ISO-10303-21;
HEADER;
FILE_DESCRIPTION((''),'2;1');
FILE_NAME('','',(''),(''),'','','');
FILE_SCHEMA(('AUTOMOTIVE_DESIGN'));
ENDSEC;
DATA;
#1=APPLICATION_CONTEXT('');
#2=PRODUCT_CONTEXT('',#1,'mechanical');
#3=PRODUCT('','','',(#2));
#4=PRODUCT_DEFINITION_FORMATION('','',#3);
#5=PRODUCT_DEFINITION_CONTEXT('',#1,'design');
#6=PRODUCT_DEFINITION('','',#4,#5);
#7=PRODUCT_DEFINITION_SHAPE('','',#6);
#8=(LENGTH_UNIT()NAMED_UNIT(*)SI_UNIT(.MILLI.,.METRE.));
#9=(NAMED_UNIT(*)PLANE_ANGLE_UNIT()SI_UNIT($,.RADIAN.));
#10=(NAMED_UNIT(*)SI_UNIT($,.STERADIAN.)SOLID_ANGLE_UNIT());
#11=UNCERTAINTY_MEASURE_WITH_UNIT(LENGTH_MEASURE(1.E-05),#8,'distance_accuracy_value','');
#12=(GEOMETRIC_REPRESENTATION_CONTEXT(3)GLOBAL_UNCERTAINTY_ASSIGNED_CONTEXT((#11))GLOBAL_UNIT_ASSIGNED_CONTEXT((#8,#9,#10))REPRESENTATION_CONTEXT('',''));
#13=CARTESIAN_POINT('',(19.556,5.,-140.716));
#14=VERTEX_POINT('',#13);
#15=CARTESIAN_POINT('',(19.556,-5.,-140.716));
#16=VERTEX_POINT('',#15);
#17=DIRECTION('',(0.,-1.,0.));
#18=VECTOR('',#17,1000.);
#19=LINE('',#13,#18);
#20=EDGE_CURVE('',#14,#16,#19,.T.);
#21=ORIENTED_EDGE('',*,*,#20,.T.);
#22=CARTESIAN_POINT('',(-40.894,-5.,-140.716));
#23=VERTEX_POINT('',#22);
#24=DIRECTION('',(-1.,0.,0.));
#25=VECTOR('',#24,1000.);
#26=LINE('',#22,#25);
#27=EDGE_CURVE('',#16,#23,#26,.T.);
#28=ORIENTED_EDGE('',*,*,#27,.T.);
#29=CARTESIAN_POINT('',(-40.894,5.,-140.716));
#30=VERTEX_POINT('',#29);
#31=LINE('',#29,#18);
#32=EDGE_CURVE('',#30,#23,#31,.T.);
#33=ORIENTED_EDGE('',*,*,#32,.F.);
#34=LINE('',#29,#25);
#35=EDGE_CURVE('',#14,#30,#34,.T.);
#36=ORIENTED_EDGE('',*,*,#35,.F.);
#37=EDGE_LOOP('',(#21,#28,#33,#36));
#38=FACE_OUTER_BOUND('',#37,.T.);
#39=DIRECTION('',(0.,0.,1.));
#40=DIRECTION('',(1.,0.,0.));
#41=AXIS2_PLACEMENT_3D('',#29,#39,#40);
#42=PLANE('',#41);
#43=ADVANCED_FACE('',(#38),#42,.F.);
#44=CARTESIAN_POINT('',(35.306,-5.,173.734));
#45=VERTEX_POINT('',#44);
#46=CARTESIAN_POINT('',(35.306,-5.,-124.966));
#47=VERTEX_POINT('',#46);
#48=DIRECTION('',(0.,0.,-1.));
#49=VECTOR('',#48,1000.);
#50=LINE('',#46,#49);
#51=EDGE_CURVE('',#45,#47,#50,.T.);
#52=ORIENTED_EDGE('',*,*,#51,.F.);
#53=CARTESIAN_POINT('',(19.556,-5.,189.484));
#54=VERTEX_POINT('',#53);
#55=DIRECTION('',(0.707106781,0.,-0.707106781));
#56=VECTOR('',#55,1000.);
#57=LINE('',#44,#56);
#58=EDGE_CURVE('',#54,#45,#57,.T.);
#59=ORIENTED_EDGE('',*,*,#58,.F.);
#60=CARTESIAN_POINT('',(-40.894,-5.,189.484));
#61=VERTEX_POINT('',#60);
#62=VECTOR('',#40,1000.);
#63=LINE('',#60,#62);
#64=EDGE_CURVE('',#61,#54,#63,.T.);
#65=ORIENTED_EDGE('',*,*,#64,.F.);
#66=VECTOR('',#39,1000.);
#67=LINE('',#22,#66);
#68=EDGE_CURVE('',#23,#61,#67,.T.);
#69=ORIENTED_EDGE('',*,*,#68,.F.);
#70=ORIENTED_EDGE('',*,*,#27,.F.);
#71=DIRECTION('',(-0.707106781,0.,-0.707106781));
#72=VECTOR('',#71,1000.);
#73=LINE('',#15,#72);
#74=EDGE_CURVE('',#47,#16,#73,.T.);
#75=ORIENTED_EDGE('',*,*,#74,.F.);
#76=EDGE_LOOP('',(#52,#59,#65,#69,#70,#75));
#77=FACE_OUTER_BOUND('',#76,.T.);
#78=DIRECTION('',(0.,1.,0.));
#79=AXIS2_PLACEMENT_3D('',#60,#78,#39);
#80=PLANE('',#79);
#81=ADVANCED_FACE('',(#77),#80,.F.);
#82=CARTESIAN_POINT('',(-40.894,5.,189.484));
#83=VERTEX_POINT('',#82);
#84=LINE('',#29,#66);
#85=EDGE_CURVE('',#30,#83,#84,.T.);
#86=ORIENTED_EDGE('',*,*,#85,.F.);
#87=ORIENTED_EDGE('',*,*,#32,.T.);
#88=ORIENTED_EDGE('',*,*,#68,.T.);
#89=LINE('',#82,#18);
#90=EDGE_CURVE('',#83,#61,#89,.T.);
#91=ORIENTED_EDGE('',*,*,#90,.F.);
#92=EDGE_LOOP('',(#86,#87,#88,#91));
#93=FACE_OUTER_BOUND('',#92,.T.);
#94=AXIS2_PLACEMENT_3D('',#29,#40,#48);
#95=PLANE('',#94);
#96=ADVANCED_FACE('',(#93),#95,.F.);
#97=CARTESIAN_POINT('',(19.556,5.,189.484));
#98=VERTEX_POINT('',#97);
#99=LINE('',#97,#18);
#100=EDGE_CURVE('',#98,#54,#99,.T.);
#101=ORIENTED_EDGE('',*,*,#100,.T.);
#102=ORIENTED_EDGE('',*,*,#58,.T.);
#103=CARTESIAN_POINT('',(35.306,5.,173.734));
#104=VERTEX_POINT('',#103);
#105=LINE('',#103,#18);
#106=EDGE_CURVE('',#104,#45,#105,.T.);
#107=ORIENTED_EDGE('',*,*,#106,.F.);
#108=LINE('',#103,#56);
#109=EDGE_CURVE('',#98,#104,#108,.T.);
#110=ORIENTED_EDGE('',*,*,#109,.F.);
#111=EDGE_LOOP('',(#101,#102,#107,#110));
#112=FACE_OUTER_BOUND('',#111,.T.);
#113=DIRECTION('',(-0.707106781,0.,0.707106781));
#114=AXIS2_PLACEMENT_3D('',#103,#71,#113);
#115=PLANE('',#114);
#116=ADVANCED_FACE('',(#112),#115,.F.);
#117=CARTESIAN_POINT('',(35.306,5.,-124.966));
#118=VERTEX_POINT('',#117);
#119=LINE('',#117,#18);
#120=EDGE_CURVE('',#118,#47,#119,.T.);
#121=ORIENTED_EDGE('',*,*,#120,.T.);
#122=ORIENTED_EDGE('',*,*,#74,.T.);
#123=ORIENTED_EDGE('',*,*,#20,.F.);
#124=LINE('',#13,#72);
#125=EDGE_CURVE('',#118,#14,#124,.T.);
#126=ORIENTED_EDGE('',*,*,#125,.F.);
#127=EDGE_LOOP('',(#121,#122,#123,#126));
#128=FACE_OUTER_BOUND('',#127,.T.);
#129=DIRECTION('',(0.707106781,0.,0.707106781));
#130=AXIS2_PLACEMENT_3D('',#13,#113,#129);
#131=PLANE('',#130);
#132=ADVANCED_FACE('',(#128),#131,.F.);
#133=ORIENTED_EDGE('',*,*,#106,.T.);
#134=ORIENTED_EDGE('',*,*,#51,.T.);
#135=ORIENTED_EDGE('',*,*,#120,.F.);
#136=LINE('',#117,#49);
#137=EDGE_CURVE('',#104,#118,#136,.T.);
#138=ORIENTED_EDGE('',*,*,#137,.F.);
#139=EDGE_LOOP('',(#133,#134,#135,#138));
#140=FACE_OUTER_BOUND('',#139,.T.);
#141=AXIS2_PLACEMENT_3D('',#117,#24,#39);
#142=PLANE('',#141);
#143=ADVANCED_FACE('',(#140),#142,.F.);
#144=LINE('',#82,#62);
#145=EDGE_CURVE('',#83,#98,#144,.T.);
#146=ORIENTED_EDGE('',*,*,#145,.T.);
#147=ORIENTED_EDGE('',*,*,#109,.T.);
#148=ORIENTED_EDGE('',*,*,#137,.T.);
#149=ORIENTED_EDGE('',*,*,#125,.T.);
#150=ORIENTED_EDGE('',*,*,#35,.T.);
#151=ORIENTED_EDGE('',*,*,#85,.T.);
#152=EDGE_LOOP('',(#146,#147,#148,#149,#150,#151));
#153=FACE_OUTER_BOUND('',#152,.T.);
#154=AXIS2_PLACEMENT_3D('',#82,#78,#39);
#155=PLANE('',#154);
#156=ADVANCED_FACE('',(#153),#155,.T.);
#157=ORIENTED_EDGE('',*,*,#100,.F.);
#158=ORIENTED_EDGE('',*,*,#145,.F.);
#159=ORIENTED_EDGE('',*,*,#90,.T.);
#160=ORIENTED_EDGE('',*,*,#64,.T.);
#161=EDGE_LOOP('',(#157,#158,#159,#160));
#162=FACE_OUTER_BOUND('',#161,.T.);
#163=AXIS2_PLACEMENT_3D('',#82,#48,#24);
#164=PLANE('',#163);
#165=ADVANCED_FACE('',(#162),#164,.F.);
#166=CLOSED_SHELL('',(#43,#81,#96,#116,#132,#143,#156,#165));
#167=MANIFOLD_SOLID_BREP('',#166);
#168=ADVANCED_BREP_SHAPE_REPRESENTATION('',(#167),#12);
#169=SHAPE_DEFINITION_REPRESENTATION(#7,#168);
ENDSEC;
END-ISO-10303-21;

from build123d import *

# Parameters (mm, degrees)
BOSS_EXTRUDE1_DEPTH = 5


with BuildPart() as part:
    # Sketch3 → Boss-Extrude1 (new, symmetric)
    with BuildSketch(Plane(origin=(0, 0, 0), x_dir=(1, 0, 0), z_dir=(0, 1, 0))):
        Polygon((19.556, 140.716), (35.306, 124.966), (35.306, -173.734), (19.556, -189.484), (-40.894, -189.484), (-40.894, 140.716), align=None)
    extrude(amount=BOSS_EXTRUDE1_DEPTH, both=True)


solid = part.part
